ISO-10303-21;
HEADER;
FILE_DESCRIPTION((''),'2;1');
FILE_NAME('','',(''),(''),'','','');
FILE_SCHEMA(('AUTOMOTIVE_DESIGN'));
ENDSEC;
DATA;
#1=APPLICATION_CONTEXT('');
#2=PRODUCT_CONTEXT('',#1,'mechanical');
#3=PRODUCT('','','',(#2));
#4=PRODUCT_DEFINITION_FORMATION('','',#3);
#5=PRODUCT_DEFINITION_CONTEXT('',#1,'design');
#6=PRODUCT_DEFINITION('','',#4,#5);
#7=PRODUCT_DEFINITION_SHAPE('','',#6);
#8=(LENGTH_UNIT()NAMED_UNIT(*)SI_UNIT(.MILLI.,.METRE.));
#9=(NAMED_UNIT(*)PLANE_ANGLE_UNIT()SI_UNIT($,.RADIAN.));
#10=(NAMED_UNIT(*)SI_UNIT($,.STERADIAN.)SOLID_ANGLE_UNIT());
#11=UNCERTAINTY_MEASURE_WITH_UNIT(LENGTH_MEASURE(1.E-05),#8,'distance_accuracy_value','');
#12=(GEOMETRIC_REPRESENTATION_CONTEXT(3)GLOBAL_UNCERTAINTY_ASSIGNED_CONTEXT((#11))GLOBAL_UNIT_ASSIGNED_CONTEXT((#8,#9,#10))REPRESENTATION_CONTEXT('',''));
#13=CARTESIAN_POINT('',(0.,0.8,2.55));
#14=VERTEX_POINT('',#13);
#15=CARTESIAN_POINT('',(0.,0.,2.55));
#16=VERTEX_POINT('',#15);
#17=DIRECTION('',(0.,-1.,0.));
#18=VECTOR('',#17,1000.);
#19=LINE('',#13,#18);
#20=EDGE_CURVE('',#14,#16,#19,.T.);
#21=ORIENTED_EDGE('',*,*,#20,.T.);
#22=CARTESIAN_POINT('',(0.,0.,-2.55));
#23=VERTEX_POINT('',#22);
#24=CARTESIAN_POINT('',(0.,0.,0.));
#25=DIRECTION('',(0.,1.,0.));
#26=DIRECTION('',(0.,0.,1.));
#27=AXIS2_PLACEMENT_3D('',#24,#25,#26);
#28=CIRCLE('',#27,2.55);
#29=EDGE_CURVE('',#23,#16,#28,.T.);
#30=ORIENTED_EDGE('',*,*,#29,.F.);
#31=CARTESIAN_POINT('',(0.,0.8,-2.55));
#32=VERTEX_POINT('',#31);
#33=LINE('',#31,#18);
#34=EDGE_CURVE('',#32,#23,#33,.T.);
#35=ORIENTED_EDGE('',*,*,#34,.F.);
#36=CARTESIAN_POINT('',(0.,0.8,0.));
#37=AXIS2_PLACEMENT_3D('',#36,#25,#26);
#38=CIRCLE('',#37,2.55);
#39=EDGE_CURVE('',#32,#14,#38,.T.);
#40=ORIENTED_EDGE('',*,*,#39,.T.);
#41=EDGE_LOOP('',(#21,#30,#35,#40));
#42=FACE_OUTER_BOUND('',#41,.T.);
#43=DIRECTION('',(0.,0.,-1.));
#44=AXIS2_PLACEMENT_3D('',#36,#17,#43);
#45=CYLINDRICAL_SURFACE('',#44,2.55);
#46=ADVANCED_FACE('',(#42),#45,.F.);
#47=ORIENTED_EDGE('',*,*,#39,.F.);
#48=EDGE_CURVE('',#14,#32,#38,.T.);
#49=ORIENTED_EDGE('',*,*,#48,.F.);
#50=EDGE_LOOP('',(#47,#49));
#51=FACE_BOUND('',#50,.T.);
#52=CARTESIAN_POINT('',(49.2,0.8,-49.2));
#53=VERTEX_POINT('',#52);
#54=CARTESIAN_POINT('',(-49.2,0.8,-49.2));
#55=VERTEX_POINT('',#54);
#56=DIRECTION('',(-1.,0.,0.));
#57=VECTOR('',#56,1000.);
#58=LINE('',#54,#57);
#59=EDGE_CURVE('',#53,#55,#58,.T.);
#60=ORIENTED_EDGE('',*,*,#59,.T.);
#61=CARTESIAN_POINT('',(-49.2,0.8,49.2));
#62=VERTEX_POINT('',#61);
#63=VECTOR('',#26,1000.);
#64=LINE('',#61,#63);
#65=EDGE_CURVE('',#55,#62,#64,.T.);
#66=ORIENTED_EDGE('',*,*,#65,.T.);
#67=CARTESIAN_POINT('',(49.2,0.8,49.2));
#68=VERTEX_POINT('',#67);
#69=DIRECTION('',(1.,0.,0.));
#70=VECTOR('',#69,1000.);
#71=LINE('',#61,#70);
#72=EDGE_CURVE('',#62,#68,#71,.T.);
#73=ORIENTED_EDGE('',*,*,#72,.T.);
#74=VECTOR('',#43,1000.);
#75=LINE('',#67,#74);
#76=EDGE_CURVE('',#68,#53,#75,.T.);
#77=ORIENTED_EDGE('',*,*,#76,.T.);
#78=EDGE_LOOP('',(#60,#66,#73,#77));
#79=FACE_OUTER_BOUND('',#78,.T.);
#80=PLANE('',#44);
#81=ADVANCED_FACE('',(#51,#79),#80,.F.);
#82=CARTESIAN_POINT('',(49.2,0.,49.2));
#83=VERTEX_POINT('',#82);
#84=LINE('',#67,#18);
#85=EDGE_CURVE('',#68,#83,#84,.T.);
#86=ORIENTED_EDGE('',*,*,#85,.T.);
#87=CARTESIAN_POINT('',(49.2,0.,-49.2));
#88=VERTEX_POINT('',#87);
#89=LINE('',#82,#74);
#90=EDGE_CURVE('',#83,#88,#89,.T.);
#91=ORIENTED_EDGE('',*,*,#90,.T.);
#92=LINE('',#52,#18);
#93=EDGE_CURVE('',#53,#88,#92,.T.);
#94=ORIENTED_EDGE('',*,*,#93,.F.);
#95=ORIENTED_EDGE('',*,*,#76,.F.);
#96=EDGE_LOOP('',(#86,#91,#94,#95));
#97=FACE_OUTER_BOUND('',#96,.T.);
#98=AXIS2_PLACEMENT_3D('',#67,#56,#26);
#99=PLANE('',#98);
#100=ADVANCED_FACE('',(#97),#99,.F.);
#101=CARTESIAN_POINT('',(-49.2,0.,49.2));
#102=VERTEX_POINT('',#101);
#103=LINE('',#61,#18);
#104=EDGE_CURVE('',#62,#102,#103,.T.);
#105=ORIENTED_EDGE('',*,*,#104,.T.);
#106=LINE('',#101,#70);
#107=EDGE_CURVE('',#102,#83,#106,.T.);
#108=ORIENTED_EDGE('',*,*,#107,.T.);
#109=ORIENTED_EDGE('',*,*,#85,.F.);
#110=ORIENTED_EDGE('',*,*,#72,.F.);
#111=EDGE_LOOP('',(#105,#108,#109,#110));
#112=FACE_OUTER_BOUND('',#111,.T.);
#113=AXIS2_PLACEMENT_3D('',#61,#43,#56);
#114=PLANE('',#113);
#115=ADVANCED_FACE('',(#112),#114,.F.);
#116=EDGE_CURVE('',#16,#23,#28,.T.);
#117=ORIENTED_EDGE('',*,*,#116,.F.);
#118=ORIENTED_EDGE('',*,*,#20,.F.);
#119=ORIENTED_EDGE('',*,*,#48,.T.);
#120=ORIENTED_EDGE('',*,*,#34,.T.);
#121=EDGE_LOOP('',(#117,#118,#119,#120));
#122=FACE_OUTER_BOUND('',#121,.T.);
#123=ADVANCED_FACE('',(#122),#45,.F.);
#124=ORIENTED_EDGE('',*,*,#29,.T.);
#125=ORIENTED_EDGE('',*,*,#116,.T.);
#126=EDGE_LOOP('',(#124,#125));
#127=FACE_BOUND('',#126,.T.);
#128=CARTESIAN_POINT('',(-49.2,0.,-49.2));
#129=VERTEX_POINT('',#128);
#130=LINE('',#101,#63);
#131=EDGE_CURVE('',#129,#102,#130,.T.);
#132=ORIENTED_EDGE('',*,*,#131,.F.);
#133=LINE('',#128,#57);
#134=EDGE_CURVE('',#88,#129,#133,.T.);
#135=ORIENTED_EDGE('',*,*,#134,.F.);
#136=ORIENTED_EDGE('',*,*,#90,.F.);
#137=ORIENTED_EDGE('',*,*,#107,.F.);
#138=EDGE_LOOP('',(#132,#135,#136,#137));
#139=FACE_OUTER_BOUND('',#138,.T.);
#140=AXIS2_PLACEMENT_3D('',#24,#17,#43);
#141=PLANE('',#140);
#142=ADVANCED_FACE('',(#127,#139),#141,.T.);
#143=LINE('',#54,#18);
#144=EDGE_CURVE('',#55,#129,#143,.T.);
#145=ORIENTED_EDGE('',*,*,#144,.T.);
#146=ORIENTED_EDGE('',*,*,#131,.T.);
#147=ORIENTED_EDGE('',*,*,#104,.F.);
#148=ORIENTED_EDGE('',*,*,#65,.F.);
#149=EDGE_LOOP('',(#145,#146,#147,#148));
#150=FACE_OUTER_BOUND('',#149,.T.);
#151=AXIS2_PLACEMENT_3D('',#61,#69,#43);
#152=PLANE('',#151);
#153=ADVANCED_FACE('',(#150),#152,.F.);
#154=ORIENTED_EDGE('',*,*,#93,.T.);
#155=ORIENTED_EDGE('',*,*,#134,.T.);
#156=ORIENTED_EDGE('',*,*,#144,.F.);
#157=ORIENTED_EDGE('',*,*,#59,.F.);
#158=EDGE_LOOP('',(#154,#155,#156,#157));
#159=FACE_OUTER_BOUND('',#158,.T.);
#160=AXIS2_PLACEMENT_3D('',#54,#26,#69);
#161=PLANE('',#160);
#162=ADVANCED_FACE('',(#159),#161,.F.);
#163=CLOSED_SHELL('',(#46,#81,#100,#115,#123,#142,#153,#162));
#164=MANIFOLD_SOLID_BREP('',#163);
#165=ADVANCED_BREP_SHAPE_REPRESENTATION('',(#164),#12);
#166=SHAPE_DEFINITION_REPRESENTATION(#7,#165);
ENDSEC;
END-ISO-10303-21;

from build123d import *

# Parameters (mm, degrees)
SKETCH1_W           = 98.4
SKETCH1_H           = 98.4
SKETCH1_R           = 2.55
BOSS_EXTRUDE1_DEPTH = 0.8


with BuildPart() as part:
    # Sketch1 → Boss-Extrude1 (new body)
    with BuildSketch(Plane(origin=(0, 0, 0), x_dir=(1, 0, 0), z_dir=(0, 1, 0))):
        Rectangle(SKETCH1_W, SKETCH1_H)
        with Locations(Location((0, 0, 0), (0, 0, 270))):
            Circle(SKETCH1_R, mode=Mode.SUBTRACT)
    extrude(amount=BOSS_EXTRUDE1_DEPTH)


solid = part.part
